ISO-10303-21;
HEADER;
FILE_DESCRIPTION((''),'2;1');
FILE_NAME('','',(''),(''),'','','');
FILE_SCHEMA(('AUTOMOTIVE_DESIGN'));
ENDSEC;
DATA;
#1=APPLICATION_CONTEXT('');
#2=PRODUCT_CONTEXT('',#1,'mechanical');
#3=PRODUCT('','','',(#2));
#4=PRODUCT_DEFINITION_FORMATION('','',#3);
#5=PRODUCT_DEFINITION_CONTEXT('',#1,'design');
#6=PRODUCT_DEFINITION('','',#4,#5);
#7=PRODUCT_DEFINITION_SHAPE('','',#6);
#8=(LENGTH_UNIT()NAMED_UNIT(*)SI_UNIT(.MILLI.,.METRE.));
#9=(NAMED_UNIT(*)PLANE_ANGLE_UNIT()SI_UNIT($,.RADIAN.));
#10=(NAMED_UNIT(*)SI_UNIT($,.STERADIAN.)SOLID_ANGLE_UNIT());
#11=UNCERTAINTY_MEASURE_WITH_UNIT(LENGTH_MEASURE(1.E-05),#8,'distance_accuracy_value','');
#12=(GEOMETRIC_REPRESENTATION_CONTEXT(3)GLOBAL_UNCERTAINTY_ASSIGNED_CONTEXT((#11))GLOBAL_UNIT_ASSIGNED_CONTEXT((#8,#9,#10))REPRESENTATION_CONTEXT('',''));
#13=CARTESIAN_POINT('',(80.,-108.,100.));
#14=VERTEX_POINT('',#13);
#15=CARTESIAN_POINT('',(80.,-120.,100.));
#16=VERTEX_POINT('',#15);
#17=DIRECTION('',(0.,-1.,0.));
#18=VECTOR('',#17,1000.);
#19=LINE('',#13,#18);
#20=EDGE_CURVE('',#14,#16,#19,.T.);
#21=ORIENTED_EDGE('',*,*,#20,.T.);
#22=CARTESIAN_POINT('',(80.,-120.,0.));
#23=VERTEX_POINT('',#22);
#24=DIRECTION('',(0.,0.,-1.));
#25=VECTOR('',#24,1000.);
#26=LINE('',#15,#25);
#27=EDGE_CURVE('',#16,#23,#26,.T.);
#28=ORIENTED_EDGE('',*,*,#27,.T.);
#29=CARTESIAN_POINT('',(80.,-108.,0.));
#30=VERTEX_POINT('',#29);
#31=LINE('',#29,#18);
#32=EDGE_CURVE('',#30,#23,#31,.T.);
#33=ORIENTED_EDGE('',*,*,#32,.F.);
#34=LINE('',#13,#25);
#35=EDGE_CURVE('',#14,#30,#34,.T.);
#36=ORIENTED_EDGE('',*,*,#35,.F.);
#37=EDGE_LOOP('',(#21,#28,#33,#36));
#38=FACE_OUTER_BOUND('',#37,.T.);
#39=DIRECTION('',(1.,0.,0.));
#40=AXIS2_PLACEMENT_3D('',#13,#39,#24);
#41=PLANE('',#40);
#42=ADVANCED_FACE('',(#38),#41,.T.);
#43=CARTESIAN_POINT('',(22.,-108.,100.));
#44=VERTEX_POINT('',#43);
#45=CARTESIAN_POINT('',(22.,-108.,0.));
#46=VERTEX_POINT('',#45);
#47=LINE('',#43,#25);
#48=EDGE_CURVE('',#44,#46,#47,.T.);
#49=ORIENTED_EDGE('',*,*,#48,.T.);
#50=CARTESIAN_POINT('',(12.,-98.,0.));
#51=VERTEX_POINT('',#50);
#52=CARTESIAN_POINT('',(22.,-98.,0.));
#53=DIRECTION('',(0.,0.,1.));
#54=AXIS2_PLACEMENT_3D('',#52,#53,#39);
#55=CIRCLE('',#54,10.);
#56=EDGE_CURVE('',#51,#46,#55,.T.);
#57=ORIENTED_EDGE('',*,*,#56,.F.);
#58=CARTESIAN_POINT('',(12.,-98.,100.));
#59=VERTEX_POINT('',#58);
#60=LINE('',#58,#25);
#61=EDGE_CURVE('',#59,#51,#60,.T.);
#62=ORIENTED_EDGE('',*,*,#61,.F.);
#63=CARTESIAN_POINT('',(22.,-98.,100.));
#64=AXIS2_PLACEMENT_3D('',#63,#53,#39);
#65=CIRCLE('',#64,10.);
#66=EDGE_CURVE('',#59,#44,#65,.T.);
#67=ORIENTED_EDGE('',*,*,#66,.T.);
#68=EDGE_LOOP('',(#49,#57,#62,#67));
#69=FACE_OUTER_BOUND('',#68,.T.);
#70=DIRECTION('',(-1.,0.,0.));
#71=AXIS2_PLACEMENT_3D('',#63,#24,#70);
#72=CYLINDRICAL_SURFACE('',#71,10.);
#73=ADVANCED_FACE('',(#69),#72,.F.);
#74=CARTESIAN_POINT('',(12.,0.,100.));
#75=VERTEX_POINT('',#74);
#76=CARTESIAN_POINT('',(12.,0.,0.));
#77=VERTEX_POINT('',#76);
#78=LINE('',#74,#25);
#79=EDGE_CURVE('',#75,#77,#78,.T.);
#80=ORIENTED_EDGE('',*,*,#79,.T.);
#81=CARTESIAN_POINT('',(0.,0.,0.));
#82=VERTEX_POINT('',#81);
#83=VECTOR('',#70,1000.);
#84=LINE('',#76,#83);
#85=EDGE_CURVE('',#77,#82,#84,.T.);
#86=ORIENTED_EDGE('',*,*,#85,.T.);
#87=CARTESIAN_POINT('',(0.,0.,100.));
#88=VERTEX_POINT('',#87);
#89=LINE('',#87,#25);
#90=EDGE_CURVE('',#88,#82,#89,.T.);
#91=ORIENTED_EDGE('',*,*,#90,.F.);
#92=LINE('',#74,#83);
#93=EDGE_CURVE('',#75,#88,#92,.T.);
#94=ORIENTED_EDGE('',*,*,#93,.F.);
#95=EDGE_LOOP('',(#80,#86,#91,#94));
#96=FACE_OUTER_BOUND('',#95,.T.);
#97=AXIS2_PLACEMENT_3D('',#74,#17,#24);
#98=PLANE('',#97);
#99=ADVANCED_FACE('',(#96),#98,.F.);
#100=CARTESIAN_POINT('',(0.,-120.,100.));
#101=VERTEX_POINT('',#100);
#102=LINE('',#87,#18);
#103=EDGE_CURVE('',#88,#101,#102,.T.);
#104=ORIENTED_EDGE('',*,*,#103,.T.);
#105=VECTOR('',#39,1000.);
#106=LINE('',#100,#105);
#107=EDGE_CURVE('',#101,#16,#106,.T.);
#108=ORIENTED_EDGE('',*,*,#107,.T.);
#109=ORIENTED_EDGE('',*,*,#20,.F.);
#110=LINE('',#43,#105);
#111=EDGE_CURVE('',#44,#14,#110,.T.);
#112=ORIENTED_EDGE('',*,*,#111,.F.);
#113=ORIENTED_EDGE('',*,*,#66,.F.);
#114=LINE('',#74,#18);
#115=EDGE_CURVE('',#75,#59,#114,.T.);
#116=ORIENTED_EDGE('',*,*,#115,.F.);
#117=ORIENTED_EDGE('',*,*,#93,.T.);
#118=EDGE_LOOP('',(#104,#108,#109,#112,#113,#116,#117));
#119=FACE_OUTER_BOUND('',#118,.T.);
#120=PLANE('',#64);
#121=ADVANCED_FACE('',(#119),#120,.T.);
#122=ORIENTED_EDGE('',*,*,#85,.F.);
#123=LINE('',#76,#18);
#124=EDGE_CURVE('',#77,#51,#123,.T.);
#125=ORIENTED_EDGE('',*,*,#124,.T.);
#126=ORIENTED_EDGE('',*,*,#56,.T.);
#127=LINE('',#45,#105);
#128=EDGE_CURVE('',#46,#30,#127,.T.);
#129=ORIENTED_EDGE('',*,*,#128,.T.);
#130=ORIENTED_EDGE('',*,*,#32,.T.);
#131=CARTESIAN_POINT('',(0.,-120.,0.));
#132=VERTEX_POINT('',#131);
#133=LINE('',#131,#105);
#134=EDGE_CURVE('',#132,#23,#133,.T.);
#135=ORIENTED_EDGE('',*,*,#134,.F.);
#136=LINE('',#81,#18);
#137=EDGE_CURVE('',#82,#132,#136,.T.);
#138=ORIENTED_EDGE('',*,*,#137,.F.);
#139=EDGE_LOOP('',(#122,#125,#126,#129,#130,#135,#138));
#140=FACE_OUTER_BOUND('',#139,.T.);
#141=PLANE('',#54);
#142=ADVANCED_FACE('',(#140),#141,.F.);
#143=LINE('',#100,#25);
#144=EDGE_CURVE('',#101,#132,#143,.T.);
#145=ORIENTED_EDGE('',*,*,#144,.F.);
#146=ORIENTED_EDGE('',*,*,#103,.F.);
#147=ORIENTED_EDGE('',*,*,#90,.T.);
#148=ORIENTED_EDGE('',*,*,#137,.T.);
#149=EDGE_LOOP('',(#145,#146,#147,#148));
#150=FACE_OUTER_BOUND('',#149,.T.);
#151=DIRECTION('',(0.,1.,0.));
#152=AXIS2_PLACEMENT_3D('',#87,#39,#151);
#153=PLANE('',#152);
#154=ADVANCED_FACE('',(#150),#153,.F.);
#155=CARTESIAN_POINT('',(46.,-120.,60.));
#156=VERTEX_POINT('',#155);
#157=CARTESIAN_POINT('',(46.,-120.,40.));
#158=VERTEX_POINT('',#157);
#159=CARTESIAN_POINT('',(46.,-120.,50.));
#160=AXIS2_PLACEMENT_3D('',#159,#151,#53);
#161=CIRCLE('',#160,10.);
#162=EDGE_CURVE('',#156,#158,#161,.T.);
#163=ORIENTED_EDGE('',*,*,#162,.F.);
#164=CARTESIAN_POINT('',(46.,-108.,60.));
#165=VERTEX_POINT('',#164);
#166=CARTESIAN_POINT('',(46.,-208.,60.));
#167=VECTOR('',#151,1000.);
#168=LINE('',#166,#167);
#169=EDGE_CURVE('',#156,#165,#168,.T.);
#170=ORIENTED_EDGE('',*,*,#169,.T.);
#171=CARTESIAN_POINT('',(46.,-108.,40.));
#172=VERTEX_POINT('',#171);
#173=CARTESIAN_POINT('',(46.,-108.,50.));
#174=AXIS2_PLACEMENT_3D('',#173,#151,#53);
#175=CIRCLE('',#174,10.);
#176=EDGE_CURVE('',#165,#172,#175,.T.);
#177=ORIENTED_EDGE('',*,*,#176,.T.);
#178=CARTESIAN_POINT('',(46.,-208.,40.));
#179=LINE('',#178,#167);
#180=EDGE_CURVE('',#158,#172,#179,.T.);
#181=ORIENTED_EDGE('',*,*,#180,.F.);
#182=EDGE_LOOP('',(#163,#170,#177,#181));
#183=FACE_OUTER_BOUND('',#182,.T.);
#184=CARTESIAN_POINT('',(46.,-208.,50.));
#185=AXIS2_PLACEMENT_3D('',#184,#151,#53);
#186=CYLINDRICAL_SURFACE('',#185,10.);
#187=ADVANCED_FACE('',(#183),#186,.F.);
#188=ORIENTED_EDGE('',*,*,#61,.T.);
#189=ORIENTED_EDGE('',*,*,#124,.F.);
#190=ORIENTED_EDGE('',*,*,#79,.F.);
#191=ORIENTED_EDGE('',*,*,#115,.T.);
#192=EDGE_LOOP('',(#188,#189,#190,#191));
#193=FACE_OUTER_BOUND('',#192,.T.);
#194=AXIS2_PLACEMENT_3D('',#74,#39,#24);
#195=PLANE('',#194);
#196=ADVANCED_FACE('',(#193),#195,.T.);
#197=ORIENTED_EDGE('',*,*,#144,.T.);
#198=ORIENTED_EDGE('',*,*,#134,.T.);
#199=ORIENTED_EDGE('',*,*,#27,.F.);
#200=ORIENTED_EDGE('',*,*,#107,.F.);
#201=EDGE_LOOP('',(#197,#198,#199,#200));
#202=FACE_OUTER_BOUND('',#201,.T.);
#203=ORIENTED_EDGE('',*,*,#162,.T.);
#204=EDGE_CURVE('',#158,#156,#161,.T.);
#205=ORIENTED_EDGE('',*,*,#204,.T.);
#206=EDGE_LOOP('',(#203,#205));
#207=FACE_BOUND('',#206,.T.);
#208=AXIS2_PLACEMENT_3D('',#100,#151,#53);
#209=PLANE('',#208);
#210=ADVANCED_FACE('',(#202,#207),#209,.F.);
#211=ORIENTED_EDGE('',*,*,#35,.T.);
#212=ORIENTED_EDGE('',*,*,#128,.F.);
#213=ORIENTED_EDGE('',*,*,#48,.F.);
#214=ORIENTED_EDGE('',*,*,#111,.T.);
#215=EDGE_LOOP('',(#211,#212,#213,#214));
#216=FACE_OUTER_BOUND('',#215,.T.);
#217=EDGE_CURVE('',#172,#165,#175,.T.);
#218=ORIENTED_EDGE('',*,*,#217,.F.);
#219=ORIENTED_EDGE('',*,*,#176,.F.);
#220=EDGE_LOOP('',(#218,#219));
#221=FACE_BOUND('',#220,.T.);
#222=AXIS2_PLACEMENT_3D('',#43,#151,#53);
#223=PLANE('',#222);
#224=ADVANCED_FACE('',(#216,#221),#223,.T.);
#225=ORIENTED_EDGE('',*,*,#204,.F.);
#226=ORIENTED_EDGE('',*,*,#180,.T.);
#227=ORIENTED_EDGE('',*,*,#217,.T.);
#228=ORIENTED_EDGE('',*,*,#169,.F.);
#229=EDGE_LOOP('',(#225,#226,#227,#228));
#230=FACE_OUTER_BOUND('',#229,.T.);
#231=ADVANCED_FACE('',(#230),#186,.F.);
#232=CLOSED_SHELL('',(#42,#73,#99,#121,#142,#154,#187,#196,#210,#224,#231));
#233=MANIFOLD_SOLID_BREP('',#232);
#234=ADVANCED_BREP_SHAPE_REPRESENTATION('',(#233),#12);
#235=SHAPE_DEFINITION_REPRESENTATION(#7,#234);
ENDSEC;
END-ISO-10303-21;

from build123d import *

# Parameters (mm, degrees)
BOSS_EXTRUDE1_DEPTH = 100
SKETCH2_R           = 10
CUT_EXTRUDE1_DEPTH  = 100


with BuildPart() as part:
    # Sketch1 → Boss-Extrude1 (new body)
    with BuildSketch(Plane.XY):
        with BuildLine():
            Line((0, 0), (0, -120))
            Line((0, -120), (80, -120))
            Line((80, -120), (80, -108))
            Line((80, -108), (22, -108))
            ThreePointArc((22, -108), (14.928932188, -105.071067812), (12, -98))
            Line((12, -98), (12, 0))
            Line((12, 0), (0, 0))
        make_face()
    extrude(amount=BOSS_EXTRUDE1_DEPTH)

    # Sketch2 → Cut-Extrude1 (cut)
    with BuildSketch(Plane(origin=(0, -108, 0), x_dir=(1, 0, 0), z_dir=(0, 1, 0))):
        with Locations(Location((46, -50, 0), (0, 0, 270))):
            Circle(SKETCH2_R)
    extrude(amount=-CUT_EXTRUDE1_DEPTH, mode=Mode.SUBTRACT)


solid = part.part
